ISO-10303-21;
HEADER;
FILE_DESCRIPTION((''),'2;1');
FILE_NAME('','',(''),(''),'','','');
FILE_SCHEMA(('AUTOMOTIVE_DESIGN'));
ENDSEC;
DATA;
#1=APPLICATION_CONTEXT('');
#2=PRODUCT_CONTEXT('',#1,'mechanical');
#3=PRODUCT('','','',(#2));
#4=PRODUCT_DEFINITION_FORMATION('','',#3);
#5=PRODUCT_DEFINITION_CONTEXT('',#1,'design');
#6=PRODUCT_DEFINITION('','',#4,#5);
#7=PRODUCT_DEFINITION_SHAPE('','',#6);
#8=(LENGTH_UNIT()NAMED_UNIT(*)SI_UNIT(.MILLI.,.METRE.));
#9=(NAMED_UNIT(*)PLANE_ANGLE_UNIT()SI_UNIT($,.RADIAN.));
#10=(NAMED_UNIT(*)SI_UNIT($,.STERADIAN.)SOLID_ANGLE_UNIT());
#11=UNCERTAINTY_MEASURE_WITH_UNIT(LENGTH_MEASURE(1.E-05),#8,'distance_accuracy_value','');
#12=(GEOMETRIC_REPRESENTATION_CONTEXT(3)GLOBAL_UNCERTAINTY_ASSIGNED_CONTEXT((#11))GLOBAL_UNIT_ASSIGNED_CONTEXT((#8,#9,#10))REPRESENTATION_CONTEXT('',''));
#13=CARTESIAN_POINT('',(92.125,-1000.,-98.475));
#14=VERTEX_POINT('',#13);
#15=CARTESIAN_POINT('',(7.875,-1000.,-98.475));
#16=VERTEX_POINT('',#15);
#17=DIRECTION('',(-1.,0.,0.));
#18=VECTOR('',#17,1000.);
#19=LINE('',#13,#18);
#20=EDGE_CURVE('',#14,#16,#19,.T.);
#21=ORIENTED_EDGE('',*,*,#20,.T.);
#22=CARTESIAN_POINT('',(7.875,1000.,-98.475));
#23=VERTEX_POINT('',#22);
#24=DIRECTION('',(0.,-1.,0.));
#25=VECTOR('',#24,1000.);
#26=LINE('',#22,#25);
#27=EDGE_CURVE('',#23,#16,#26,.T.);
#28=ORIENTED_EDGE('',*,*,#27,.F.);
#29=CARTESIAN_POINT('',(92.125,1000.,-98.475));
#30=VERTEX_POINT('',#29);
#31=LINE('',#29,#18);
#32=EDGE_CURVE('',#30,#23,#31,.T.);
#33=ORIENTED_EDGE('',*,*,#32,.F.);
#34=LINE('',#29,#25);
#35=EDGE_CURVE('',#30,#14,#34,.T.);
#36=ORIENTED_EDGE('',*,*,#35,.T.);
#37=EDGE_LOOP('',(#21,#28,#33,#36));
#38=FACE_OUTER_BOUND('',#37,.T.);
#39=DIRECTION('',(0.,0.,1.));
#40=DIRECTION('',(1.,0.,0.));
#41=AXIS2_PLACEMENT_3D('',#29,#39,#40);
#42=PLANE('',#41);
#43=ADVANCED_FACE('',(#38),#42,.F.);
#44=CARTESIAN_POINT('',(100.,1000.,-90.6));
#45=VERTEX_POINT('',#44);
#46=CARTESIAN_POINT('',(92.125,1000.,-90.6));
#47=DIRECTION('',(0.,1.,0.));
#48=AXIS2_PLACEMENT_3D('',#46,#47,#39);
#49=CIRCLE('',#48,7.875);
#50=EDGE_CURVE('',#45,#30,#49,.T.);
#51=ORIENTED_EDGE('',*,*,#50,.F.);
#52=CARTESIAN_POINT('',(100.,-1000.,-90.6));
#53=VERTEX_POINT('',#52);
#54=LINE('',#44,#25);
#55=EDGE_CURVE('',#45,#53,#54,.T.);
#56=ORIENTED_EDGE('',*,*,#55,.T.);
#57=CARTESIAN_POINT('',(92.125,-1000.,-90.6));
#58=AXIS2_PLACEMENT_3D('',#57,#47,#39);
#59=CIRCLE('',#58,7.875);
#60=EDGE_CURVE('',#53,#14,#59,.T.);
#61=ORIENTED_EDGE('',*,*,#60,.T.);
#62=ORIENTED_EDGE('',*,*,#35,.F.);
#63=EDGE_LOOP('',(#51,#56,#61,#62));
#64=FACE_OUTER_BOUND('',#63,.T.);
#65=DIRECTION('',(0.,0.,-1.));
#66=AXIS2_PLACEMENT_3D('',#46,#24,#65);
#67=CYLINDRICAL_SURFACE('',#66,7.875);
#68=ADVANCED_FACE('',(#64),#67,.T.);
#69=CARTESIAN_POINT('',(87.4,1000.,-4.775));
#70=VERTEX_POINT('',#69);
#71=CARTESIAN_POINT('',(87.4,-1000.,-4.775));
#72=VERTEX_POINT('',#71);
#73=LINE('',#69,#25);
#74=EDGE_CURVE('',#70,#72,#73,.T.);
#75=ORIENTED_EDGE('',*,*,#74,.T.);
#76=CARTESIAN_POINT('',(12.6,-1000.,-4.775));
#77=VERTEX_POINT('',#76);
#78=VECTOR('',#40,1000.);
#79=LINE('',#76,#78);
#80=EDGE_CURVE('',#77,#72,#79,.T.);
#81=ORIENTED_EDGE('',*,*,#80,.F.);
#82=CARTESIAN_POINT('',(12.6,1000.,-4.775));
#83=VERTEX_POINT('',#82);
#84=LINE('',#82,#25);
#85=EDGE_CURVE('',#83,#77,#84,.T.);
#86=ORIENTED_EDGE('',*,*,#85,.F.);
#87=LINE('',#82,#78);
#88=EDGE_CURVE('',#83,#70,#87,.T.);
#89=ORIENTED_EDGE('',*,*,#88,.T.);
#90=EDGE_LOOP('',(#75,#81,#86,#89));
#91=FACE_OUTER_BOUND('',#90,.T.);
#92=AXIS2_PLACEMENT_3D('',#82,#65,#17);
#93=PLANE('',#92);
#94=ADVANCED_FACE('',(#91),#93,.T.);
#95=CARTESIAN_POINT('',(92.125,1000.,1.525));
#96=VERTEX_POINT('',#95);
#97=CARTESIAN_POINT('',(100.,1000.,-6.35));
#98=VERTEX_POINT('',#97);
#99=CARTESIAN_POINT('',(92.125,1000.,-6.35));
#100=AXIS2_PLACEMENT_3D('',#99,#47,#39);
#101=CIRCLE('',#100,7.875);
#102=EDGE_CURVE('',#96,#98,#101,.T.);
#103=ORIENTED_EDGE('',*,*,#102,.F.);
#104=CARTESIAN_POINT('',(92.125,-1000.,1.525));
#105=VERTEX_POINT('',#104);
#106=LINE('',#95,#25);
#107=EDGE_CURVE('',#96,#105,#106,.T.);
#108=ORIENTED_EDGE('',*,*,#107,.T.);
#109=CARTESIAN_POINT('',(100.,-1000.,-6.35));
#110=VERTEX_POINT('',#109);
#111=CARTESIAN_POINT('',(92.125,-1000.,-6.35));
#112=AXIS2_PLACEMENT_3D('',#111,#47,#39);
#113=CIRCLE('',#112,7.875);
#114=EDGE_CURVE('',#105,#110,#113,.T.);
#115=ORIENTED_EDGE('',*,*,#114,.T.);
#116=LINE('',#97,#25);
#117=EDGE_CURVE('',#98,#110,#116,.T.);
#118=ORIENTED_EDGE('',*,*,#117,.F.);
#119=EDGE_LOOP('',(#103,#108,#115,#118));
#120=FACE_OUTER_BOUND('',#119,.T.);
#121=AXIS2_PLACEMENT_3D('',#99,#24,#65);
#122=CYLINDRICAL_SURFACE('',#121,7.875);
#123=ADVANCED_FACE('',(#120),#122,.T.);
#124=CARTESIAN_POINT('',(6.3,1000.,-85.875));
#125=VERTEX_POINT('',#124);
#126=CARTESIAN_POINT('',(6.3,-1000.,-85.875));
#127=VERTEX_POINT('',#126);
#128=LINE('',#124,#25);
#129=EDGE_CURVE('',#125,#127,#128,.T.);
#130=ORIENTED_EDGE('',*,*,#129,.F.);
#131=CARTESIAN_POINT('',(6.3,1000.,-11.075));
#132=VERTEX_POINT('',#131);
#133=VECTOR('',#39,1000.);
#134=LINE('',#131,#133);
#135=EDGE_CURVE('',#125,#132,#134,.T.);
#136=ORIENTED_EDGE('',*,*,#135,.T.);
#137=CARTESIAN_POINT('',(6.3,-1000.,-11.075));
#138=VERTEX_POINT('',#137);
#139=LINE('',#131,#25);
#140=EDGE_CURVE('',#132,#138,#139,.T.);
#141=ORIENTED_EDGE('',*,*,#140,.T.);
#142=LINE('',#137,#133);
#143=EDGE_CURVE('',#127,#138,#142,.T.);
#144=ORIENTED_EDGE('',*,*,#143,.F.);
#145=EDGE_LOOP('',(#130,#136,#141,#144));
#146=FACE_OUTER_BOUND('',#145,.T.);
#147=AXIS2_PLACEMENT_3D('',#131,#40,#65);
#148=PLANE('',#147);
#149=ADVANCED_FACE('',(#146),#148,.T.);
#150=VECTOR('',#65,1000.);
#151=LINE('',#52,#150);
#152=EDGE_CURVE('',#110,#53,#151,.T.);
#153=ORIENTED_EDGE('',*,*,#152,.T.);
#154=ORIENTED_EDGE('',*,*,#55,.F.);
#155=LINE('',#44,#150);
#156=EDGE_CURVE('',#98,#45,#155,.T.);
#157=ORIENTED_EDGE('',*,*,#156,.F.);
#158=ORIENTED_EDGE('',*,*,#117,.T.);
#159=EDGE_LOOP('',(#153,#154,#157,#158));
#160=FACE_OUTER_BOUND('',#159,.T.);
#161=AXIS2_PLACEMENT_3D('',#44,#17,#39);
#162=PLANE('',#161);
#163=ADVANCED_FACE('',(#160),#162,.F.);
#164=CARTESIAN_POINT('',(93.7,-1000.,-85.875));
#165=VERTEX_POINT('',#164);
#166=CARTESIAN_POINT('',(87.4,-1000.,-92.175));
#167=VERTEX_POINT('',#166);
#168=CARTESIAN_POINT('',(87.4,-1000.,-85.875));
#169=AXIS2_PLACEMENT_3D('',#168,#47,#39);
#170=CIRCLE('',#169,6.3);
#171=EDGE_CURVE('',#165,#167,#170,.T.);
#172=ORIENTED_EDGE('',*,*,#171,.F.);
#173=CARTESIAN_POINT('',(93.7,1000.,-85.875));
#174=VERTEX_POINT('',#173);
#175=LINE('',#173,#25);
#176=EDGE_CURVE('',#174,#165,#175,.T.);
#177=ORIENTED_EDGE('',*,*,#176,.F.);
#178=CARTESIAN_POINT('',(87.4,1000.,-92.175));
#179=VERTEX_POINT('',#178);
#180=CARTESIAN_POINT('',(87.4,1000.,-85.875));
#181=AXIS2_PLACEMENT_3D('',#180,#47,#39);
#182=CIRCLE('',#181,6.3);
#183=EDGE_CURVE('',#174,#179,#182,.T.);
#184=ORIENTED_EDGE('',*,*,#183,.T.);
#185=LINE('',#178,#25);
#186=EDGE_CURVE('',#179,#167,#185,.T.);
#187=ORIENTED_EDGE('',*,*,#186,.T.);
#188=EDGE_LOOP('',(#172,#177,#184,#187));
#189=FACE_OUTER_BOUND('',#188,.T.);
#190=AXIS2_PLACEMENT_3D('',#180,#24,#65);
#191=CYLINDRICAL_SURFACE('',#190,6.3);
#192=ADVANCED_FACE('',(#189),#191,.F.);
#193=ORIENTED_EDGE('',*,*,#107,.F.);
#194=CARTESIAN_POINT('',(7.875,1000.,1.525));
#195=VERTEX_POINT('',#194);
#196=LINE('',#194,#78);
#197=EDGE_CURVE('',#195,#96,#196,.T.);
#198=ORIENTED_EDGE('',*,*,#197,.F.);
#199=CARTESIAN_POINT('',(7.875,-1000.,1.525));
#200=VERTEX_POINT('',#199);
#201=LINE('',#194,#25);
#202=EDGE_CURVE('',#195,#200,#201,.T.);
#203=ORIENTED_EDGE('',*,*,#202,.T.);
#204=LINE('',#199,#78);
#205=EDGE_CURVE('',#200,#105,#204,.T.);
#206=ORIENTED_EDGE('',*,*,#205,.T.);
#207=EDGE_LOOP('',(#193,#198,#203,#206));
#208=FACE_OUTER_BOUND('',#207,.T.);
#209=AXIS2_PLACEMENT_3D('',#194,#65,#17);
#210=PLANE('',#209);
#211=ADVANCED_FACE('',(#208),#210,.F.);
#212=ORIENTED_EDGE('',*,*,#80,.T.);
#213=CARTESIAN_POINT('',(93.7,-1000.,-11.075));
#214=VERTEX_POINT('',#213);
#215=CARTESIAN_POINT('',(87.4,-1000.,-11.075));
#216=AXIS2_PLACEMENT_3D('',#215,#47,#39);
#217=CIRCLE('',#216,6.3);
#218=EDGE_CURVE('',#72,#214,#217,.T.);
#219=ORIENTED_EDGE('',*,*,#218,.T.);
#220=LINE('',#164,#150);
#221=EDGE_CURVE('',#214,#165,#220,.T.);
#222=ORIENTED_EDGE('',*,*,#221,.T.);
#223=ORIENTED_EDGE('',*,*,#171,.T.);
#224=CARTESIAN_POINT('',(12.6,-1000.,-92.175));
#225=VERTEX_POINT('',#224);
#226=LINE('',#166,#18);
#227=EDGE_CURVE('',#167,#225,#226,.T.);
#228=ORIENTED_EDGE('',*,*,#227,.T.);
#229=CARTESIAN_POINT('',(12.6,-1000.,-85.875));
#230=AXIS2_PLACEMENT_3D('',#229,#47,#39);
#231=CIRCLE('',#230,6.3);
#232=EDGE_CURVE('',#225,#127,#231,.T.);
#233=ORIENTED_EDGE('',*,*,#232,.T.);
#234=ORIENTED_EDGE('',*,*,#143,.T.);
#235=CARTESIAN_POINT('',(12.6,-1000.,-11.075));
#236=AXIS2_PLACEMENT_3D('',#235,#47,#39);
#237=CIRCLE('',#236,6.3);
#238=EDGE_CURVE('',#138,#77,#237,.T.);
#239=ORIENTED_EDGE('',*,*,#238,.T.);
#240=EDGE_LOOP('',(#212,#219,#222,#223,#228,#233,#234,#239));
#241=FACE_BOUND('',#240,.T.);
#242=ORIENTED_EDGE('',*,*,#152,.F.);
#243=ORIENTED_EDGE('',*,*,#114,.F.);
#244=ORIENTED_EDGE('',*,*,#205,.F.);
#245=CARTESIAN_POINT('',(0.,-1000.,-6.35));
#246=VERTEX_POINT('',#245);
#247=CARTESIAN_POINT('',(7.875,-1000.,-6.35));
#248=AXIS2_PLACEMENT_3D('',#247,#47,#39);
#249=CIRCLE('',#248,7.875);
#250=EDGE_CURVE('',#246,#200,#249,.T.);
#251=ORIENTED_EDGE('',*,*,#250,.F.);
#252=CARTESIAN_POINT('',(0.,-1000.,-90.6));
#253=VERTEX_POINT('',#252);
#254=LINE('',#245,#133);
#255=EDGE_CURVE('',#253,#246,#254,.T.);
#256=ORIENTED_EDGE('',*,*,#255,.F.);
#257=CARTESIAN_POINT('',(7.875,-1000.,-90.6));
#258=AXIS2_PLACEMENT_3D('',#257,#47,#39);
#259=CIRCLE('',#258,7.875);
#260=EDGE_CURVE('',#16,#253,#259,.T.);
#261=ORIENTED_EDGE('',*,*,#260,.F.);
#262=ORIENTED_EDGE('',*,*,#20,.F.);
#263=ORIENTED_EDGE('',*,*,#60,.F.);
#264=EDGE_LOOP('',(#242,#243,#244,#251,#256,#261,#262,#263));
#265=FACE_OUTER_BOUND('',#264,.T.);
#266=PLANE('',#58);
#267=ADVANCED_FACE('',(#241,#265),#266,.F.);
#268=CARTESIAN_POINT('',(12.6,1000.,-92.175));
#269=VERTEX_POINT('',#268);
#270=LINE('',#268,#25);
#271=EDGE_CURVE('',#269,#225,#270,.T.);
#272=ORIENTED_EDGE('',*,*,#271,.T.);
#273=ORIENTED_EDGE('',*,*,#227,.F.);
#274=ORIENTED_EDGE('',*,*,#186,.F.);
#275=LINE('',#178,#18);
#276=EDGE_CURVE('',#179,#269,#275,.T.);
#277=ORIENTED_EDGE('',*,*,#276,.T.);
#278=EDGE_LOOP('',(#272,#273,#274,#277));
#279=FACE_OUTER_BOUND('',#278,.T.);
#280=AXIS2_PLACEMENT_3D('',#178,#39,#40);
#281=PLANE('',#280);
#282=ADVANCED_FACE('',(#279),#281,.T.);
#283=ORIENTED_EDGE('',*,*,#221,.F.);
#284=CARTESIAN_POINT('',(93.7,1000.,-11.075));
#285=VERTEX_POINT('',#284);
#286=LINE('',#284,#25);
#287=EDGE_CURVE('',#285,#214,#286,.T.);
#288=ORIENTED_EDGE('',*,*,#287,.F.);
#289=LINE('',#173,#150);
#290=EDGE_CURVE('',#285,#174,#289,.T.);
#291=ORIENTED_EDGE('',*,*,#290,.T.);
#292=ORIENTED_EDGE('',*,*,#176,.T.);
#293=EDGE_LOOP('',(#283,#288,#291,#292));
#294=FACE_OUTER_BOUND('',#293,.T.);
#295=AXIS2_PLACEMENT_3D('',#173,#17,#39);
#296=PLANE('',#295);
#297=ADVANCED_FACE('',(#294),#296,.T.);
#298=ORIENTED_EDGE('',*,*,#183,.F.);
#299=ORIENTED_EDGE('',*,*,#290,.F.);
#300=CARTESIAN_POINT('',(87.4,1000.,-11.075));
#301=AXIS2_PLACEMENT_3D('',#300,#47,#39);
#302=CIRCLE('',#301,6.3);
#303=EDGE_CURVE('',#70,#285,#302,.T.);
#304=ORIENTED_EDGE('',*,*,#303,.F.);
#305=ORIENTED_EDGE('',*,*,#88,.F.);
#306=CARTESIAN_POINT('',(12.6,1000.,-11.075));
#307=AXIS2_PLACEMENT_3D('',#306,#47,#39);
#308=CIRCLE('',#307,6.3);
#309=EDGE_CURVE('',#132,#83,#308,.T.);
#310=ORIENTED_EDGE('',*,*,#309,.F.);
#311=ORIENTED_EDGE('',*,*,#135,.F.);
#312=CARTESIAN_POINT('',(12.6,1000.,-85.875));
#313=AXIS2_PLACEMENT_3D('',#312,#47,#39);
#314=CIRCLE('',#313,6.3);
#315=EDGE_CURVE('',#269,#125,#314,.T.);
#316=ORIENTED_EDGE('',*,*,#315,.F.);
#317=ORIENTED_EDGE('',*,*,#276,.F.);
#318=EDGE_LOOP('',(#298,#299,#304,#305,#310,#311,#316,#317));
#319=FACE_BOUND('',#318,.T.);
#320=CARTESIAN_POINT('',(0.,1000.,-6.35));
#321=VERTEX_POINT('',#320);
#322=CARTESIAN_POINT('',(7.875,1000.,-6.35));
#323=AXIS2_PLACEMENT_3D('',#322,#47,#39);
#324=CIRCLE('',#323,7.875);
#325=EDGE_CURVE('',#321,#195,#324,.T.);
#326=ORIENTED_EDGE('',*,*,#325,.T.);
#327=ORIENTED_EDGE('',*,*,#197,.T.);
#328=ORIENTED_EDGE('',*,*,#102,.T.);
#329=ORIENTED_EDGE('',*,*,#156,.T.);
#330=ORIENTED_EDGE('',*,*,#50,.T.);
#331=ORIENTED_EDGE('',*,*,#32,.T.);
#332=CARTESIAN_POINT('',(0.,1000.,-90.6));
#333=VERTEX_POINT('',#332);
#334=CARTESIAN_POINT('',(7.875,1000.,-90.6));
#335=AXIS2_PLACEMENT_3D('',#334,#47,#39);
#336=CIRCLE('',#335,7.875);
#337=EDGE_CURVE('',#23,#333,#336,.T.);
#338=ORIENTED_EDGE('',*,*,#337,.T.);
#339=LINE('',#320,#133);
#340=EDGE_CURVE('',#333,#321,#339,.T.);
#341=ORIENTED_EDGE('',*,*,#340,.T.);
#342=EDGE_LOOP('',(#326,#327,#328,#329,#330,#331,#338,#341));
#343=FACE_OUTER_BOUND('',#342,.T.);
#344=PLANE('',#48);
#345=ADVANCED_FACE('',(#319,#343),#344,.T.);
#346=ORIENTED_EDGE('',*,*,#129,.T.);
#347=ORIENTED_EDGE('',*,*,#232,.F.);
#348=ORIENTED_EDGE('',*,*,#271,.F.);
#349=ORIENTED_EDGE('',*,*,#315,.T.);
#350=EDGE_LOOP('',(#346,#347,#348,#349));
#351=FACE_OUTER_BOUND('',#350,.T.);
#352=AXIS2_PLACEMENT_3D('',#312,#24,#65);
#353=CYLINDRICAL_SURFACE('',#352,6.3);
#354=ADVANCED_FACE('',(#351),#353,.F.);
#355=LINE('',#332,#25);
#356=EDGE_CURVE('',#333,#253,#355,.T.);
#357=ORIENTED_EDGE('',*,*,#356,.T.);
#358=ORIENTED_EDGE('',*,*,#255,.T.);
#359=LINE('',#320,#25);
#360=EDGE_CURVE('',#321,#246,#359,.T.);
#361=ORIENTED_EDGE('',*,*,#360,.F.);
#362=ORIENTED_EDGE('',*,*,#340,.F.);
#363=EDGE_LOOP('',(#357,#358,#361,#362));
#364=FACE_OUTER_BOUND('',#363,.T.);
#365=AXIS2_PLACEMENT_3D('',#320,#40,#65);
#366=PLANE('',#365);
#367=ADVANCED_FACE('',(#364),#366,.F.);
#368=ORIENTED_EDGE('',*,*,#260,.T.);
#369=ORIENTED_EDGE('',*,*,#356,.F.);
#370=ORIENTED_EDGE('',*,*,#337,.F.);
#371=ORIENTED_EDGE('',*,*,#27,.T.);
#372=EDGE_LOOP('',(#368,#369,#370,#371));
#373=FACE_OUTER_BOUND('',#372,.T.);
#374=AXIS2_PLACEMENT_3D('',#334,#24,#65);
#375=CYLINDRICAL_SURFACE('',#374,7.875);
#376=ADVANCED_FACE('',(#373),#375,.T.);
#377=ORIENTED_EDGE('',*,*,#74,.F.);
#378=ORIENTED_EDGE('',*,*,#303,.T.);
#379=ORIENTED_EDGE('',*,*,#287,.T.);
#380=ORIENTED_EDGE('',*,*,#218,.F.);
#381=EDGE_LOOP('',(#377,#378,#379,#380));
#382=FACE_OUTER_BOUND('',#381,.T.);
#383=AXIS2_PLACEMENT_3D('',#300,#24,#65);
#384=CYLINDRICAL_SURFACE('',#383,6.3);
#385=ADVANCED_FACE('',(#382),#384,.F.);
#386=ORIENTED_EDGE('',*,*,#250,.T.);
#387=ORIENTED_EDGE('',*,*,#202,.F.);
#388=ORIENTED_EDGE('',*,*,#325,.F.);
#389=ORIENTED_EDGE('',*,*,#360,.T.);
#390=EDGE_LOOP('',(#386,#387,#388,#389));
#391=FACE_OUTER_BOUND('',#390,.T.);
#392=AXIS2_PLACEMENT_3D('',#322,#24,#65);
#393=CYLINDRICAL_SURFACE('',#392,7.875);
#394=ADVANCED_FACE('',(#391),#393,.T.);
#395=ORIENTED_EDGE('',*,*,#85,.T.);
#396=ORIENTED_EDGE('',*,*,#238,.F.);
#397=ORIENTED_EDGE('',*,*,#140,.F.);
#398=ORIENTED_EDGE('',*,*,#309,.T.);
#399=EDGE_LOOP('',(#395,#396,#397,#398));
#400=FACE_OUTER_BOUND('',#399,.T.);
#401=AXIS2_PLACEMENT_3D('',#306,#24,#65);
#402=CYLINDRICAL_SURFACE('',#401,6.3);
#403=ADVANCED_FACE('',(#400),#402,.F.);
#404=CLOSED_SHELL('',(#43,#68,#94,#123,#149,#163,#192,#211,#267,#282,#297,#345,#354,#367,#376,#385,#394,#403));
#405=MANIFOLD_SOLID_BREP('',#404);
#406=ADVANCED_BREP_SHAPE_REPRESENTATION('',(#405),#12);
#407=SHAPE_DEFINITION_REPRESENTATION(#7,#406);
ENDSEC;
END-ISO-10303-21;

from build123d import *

# Parameters (mm, degrees)
BOSS_EXTRUDE1_DEPTH = 1000


with BuildPart() as part:
    # Sketch2 → Boss-Extrude1 (new, symmetric)
    with BuildSketch(Plane(origin=(0, 0, 0), x_dir=(1, 0, 0), z_dir=(0, 1, 0))):
        with BuildLine():
            Line((7.875, -1.525), (92.125, -1.525))
            ThreePointArc((92.125, -1.525), (97.693465902, 0.781534098), (100, 6.35))
            Line((100, 6.35), (100, 90.6))
            ThreePointArc((100, 90.6), (97.693465902, 96.168465902), (92.125, 98.475))
            Line((92.125, 98.475), (7.875, 98.475))
            ThreePointArc((7.875, 98.475), (2.306534098, 96.168465902), (0, 90.6))
            Line((0, 90.6), (0, 6.35))
            ThreePointArc((0, 6.35), (2.306534098, 0.781534098), (7.875, -1.525))
        make_face()
        with BuildLine():
            Line((12.6, 4.775), (87.4, 4.775))
            ThreePointArc((87.4, 4.775), (91.854772721, 6.620227279), (93.7, 11.075))
            Line((93.7, 11.075), (93.7, 85.875))
            ThreePointArc((93.7, 85.875), (91.854772721, 90.329772721), (87.4, 92.175))
            Line((87.4, 92.175), (12.6, 92.175))
            ThreePointArc((12.6, 92.175), (8.145227279, 90.329772721), (6.3, 85.875))
            Line((6.3, 85.875), (6.3, 11.075))
            ThreePointArc((6.3, 11.075), (8.145227279, 6.620227279), (12.6, 4.775))
        make_face(mode=Mode.SUBTRACT)
    extrude(amount=BOSS_EXTRUDE1_DEPTH, both=True)


solid = part.part
